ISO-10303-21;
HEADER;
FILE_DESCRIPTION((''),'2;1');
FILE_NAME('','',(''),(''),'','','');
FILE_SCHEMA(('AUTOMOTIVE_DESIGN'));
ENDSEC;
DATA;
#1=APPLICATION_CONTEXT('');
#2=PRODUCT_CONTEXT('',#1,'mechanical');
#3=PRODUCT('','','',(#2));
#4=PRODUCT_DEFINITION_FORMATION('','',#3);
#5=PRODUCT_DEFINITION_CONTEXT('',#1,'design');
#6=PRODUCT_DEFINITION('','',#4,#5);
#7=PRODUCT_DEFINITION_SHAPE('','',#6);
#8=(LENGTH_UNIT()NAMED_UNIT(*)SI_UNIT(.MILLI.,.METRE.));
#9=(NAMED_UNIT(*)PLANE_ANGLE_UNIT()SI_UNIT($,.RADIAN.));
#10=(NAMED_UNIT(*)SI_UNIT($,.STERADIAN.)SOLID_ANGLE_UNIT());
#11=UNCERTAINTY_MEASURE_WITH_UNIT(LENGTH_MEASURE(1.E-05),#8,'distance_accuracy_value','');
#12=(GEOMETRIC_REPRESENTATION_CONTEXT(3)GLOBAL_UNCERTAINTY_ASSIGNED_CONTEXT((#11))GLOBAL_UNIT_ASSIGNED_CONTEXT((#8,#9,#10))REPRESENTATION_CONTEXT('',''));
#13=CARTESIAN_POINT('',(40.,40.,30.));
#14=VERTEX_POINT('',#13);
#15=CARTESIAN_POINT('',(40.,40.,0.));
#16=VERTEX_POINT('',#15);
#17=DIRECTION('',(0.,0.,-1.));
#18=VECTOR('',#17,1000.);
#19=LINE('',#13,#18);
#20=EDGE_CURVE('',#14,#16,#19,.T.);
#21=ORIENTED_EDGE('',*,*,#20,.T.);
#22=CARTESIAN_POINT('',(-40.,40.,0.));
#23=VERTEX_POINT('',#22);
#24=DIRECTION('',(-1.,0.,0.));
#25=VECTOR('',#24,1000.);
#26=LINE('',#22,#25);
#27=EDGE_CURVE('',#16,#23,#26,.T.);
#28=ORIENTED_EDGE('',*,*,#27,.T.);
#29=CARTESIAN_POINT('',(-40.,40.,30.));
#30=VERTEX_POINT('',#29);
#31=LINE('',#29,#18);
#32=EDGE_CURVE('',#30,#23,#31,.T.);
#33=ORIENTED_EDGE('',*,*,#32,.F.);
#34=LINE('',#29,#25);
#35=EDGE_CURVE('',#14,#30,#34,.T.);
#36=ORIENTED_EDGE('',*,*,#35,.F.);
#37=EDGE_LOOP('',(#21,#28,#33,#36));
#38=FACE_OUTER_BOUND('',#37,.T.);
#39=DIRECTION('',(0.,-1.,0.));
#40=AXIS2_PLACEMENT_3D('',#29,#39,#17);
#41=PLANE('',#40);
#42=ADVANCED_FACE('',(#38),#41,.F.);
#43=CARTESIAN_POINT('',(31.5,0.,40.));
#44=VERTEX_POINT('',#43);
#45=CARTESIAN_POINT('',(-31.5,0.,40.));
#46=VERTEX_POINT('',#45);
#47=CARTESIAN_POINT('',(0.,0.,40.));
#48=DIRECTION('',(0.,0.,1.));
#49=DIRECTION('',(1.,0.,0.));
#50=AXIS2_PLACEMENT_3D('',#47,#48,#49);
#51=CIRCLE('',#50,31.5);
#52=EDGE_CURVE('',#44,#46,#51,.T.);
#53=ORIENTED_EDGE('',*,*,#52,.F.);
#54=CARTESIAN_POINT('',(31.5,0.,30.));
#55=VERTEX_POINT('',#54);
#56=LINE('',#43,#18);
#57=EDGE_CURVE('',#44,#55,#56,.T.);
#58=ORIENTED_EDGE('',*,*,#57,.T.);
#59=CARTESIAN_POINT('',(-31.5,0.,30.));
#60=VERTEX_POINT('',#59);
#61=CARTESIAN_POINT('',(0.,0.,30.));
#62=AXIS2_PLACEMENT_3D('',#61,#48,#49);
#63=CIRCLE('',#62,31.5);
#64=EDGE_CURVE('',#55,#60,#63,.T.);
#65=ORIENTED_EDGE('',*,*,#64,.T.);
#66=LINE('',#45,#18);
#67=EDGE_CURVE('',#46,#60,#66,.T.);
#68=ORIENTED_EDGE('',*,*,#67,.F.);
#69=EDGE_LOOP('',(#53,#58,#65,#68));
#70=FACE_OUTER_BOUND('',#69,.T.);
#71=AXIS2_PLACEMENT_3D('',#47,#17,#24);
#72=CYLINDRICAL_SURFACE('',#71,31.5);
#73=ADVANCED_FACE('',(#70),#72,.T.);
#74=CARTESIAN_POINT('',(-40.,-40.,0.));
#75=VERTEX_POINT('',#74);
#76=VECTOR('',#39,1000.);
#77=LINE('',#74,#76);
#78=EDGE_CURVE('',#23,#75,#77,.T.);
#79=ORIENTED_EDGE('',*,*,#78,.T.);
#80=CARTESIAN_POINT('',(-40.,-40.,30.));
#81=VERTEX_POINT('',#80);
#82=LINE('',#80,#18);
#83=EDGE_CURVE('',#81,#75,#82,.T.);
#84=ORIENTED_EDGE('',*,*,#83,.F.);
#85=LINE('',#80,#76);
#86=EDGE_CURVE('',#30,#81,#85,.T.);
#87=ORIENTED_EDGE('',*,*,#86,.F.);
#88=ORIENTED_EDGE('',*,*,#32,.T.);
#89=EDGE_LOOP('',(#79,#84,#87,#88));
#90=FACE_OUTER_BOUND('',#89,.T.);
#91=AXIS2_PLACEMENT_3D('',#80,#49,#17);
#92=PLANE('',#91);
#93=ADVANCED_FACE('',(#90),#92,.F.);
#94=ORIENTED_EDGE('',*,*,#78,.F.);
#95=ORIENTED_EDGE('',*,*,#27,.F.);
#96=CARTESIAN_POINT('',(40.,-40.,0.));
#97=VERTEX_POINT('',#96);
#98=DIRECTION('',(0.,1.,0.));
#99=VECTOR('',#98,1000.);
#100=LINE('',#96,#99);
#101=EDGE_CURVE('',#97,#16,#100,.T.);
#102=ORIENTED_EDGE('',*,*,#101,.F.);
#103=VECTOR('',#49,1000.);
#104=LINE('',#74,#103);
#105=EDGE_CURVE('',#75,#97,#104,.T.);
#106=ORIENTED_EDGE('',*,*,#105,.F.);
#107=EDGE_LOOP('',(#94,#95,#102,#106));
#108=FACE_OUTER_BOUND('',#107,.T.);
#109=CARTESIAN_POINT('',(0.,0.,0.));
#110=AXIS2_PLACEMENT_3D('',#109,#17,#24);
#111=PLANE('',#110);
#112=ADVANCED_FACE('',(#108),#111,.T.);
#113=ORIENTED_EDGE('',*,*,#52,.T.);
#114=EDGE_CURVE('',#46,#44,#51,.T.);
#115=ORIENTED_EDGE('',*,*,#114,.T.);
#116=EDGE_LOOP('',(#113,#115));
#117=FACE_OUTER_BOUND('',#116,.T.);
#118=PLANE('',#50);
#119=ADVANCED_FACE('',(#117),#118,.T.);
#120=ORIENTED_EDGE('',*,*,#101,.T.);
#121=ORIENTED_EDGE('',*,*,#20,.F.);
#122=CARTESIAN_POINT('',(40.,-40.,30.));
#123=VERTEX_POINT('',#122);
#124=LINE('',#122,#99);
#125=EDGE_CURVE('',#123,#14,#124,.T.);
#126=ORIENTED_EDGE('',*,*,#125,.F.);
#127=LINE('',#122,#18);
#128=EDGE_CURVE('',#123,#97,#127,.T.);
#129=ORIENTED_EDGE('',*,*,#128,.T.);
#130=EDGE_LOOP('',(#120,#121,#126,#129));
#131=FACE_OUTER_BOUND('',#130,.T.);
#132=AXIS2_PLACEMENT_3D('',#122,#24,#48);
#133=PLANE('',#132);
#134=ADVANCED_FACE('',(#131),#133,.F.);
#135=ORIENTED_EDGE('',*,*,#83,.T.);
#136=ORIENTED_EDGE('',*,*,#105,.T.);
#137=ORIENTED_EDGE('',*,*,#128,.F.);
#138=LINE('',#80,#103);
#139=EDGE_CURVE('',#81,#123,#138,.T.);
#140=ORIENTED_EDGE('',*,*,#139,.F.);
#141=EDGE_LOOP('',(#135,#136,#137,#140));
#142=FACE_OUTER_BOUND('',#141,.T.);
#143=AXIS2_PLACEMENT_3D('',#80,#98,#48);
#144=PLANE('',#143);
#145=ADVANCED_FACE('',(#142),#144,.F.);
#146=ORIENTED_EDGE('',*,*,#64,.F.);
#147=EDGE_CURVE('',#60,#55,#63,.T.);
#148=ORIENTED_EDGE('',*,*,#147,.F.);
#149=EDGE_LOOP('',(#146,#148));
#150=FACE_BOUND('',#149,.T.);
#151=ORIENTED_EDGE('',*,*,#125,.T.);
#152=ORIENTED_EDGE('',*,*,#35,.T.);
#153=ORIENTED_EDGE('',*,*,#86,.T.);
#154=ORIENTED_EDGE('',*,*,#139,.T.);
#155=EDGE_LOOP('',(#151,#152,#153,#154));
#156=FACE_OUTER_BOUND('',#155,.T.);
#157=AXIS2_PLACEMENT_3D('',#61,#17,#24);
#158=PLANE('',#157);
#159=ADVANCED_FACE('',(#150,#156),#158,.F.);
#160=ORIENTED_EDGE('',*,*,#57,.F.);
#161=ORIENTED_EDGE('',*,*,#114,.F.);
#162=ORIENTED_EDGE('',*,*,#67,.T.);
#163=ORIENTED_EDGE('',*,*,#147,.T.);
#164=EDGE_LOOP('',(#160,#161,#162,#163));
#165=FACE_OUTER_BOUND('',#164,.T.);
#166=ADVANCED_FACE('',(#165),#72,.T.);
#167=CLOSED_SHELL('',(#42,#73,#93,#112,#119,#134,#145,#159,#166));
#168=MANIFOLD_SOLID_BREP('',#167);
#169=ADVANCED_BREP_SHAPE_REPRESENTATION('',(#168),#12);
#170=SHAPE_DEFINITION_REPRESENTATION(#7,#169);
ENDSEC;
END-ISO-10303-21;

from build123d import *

# Parameters (mm, degrees)
SKETCH_1_W      = 80
SKETCH_1_H      = 80
EXTRUDE_1_DEPTH = 30
SKETCH_2_R      = 31.5
EXTRUDE_2_DEPTH = 10


with BuildPart() as part:
    # 草图1 → 凸台-拉伸1 (new body)
    with BuildSketch(Plane.XY):
        Rectangle(SKETCH_1_W, SKETCH_1_H)
    extrude(amount=EXTRUDE_1_DEPTH)

    # 草图2 → 凸台-拉伸2 (add)
    with BuildSketch(Plane.XY.offset(30)):
        Circle(SKETCH_2_R)
    extrude(amount=EXTRUDE_2_DEPTH)


solid = part.part
